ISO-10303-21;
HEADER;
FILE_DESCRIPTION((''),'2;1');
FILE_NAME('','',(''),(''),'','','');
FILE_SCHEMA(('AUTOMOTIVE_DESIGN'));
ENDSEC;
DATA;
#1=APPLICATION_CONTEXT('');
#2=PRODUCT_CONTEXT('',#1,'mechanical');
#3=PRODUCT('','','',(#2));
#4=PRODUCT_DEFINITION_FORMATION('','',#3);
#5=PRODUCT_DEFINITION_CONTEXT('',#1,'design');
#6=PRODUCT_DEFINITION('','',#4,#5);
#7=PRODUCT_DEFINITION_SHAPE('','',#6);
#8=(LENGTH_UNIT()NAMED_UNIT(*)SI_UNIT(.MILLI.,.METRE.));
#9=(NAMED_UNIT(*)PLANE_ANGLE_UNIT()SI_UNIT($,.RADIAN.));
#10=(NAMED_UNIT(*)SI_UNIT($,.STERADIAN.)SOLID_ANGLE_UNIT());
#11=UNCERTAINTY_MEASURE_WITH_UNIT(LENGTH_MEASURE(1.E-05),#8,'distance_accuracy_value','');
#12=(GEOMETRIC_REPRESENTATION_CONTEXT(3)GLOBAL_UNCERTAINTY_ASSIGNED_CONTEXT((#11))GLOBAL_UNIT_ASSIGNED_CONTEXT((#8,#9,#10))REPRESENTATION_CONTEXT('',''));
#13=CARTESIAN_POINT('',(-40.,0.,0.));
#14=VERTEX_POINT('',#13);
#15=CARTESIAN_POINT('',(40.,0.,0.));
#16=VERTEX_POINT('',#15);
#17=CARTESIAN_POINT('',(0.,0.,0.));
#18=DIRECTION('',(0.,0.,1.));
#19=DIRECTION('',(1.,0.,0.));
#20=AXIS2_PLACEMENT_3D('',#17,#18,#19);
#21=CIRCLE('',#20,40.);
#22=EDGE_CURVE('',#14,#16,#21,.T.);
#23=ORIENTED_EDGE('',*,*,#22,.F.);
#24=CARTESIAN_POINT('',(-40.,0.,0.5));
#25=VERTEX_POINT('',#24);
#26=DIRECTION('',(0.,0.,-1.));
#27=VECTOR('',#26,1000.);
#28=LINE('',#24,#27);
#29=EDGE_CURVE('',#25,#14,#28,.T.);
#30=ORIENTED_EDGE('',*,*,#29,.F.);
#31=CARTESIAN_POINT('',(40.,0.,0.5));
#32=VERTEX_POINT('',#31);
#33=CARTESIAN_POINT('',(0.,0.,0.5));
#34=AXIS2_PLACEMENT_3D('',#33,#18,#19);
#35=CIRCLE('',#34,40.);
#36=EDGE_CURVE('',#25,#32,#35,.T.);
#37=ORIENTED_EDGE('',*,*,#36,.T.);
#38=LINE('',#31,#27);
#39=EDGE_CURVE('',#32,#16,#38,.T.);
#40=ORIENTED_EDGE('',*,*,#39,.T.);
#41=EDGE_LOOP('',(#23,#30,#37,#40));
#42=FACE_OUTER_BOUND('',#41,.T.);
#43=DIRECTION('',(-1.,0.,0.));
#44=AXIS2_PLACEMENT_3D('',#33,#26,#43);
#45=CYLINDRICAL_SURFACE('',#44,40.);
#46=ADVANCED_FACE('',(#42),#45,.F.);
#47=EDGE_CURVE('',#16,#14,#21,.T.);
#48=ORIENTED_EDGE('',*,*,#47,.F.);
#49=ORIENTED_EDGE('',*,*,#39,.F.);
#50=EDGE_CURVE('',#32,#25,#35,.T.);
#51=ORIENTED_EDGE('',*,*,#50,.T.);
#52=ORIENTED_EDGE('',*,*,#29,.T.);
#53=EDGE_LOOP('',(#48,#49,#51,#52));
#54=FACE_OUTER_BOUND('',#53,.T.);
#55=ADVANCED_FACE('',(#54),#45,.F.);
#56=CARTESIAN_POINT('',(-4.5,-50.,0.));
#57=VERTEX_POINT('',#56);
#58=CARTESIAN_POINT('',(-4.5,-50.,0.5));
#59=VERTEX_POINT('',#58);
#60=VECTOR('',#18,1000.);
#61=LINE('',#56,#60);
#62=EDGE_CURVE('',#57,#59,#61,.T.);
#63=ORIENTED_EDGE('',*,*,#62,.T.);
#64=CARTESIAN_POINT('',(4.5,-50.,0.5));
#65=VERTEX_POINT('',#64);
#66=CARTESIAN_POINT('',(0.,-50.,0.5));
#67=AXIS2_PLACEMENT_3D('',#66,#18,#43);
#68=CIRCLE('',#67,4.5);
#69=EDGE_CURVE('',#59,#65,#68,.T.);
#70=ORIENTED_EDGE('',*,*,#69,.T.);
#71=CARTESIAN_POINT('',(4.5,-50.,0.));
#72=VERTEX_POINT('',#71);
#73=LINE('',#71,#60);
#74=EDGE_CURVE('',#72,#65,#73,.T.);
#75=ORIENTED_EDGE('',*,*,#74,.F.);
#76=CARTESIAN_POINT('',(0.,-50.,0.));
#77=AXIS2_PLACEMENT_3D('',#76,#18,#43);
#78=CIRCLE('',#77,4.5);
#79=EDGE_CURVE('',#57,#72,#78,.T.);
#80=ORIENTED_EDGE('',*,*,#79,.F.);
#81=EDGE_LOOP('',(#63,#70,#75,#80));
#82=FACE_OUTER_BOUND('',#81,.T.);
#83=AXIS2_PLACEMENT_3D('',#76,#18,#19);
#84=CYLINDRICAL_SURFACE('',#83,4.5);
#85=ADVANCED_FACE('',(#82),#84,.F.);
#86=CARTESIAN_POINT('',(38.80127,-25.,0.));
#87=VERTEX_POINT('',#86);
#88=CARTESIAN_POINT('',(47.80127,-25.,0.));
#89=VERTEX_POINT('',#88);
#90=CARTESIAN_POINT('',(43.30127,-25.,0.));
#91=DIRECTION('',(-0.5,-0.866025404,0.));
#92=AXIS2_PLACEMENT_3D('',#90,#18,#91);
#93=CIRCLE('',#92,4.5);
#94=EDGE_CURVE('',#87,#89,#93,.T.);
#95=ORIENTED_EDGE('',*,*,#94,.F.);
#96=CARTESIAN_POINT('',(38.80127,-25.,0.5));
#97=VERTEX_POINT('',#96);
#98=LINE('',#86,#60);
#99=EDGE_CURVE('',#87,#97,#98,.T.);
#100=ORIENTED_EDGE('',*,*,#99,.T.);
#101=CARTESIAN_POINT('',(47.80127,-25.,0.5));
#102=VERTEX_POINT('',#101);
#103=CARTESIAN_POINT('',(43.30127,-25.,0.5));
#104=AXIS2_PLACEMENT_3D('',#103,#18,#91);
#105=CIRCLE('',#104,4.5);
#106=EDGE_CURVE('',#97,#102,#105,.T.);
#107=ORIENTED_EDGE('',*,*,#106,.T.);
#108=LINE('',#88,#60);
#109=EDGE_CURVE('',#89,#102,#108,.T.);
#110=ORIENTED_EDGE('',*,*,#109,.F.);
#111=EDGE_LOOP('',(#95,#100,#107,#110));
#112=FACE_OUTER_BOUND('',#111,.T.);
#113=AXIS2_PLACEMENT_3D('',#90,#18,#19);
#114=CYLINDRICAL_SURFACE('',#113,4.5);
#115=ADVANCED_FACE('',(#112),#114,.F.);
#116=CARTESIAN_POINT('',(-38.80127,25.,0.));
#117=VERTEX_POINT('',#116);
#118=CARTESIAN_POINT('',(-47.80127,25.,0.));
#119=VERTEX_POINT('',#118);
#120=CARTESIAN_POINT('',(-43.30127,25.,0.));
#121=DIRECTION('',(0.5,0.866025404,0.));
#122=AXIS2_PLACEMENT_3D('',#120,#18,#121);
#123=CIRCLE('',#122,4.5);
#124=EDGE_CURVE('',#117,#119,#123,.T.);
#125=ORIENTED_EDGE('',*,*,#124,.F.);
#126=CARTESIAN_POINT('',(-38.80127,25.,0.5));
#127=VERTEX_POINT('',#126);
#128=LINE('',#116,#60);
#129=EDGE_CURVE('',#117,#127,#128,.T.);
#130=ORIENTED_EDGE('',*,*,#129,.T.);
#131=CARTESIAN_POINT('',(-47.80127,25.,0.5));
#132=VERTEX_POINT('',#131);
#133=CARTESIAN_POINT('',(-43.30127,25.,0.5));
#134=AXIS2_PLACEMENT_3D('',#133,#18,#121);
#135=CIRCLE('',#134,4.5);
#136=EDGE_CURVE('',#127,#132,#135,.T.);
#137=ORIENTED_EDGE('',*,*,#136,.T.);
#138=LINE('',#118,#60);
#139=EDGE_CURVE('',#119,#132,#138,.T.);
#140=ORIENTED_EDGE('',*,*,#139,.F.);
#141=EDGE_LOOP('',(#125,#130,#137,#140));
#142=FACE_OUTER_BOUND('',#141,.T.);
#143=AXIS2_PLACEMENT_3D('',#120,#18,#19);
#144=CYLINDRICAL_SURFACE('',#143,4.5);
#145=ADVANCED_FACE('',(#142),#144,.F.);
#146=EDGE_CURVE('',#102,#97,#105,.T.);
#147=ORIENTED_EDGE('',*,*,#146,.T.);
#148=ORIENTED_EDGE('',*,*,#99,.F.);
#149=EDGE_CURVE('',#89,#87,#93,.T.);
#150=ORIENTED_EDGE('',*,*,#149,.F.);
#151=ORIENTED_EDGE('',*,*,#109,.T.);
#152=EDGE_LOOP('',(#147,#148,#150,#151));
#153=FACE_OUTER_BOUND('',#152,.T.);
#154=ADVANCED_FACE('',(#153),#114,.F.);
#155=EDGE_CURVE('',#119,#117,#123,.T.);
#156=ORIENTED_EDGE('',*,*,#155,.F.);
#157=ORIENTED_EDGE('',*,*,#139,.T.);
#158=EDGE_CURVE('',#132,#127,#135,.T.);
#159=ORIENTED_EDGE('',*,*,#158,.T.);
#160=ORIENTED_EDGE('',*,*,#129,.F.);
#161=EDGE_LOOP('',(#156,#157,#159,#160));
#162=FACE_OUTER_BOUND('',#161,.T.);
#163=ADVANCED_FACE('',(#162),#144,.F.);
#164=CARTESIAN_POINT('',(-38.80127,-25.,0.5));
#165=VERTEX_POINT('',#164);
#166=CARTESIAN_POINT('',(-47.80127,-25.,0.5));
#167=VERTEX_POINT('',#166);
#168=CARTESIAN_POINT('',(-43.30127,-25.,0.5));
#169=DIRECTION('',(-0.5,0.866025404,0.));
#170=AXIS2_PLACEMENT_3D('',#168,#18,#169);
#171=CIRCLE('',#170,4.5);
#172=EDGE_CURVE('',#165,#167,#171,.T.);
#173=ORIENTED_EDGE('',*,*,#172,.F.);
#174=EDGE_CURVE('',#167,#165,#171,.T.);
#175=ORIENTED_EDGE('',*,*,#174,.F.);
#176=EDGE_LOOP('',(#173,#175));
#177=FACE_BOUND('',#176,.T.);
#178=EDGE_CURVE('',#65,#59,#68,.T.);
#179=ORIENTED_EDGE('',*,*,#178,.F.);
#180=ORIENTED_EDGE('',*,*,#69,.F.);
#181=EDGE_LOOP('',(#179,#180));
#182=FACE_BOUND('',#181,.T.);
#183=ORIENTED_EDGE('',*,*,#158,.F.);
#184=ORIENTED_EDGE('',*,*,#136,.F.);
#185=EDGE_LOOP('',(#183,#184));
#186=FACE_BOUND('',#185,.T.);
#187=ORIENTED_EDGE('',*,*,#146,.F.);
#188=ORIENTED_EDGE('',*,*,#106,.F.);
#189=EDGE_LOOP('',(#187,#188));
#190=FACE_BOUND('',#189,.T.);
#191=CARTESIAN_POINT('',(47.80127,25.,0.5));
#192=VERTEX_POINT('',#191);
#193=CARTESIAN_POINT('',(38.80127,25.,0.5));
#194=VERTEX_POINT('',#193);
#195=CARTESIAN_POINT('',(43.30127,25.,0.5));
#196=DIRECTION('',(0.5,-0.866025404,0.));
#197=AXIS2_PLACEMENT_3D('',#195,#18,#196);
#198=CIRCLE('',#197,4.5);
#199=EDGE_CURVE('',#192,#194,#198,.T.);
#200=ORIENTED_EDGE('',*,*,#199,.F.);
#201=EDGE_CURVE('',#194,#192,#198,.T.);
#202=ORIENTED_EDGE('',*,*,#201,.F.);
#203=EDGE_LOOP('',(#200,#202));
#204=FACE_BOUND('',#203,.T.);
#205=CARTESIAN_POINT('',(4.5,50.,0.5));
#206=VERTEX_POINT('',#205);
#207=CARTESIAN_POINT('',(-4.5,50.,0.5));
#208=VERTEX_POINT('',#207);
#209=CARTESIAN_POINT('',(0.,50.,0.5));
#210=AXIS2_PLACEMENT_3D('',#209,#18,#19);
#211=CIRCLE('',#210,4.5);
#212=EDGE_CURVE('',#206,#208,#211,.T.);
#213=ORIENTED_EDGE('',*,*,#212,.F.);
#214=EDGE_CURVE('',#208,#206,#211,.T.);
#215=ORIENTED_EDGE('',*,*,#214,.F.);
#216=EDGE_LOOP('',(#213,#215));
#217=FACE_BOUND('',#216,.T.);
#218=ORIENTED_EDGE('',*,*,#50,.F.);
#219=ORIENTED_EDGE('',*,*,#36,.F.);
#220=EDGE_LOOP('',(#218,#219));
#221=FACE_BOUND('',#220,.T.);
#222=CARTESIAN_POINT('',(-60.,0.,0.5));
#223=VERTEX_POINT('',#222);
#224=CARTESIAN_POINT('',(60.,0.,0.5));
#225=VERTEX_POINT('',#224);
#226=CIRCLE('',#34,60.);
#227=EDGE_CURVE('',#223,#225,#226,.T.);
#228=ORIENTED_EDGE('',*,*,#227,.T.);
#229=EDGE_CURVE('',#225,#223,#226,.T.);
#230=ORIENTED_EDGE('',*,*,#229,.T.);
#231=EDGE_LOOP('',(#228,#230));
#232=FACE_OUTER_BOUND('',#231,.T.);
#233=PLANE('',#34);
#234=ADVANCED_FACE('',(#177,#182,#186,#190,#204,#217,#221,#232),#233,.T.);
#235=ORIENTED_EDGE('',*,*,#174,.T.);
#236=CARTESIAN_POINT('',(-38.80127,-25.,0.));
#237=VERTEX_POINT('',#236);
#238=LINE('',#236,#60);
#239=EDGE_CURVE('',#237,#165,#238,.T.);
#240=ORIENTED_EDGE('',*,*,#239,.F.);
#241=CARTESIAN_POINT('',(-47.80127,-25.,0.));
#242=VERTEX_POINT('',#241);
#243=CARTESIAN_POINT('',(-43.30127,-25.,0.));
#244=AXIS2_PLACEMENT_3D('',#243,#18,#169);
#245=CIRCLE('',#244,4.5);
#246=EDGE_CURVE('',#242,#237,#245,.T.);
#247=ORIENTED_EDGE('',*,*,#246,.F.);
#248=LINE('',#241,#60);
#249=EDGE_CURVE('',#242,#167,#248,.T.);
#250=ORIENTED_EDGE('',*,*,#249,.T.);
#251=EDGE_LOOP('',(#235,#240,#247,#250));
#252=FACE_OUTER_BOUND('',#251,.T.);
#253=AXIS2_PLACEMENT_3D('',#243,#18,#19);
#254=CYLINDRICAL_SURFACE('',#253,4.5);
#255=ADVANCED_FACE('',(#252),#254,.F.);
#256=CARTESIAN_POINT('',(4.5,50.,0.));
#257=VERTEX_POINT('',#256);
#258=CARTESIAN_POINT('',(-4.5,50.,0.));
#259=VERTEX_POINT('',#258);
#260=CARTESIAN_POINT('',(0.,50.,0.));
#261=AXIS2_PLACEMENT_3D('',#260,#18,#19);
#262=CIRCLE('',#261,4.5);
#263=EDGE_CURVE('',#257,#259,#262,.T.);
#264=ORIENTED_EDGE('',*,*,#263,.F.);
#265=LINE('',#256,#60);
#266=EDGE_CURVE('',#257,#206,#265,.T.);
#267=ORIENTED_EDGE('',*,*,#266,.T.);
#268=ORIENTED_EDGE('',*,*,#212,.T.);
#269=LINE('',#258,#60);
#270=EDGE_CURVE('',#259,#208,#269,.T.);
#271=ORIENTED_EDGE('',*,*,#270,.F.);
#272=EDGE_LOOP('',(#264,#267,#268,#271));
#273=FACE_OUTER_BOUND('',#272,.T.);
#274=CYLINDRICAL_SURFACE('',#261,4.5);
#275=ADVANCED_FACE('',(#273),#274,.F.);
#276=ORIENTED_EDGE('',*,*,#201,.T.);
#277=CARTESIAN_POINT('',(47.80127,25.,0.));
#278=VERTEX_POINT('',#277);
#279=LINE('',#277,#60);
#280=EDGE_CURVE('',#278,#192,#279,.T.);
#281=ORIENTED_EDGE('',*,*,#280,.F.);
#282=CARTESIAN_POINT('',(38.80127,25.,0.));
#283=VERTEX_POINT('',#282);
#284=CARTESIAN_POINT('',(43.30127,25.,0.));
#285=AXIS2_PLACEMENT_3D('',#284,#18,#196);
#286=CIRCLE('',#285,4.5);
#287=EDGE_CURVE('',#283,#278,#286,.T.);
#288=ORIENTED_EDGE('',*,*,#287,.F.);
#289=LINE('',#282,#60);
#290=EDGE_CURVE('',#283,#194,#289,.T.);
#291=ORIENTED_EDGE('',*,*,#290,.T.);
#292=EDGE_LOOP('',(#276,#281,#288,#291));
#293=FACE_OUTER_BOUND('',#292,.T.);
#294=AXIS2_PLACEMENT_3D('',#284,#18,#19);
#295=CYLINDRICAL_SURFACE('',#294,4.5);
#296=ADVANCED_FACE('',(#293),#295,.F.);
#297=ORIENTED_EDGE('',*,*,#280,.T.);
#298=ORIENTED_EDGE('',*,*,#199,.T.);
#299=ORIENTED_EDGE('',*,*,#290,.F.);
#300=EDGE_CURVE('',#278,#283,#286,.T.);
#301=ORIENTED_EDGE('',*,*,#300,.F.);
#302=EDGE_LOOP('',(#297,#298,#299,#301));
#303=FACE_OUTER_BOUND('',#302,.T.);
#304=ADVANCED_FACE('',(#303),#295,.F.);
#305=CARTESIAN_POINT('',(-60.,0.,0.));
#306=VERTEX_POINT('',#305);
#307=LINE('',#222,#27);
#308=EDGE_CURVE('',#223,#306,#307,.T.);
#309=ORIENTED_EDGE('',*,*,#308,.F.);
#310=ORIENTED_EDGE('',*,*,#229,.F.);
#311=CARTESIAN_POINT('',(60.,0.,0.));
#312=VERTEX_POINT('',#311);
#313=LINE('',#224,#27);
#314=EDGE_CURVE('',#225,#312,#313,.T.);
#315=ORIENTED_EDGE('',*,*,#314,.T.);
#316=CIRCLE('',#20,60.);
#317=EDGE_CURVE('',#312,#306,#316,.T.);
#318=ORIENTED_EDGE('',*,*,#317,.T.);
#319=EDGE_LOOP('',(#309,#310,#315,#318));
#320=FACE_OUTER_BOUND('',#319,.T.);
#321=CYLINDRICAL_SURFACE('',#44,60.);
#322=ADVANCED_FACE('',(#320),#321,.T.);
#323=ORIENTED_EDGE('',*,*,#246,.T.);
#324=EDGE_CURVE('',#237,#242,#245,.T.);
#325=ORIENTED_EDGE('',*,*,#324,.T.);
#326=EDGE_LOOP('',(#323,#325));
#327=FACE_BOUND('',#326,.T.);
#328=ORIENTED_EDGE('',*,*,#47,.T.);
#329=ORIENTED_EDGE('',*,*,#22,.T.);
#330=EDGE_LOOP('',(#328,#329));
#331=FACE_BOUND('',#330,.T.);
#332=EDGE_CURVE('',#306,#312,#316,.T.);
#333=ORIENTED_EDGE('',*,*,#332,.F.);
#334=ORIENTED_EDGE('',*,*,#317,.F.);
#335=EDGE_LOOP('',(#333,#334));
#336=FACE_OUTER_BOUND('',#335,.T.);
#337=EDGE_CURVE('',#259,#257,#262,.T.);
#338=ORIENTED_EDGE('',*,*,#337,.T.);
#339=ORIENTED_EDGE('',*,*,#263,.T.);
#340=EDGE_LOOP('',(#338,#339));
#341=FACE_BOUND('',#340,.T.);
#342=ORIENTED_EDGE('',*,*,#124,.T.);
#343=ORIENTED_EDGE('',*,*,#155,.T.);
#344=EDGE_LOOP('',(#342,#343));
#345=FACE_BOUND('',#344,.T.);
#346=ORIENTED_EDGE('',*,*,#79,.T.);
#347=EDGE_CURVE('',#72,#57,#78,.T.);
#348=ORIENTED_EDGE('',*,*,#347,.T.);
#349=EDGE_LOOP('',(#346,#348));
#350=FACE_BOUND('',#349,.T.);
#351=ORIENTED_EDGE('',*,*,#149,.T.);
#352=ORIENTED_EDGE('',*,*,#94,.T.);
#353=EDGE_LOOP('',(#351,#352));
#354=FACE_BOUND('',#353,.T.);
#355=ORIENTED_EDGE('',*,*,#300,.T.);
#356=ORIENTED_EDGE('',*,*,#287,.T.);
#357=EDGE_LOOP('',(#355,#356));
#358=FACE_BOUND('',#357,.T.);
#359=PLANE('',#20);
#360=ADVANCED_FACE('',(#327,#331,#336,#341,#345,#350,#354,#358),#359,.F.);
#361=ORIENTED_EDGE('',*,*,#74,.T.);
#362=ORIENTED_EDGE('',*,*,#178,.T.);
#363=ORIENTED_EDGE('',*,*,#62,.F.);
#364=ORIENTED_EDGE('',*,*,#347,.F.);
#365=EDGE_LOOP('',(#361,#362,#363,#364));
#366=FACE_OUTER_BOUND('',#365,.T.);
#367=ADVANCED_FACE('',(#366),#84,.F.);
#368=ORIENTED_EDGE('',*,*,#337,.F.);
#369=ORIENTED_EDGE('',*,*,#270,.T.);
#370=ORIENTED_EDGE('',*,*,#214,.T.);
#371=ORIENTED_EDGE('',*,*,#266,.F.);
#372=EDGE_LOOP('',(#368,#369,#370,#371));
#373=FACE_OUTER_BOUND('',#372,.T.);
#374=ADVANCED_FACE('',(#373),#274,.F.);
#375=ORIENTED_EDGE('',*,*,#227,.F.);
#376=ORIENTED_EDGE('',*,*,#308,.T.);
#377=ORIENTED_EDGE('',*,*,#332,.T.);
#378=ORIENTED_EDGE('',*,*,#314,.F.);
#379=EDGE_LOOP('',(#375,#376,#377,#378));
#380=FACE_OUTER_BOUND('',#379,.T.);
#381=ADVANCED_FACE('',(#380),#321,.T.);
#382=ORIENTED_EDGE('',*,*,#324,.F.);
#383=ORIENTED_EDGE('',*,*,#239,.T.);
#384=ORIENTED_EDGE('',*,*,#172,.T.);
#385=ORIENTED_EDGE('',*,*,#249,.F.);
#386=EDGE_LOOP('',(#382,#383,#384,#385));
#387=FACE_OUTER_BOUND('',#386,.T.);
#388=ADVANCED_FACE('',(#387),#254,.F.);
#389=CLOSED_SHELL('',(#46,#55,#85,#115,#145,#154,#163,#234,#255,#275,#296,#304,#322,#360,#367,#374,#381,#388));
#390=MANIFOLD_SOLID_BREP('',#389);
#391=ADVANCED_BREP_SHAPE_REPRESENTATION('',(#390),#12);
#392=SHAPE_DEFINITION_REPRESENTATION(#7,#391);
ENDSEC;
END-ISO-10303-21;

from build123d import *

# Parameters (mm, degrees)
SKETCH1_R           = 60
SKETCH1_R_2         = 40
BOSS_EXTRUDE1_DEPTH = 0.5
SKETCH2_R           = 4.5
CUT_EXTRUDE1_DEPTH  = 85.854286869
CIRPATTERN1_COUNT   = 6


with BuildPart() as part:
    # Sketch1 → Boss-Extrude1 (new body)
    with BuildSketch(Plane.XY):
        Circle(SKETCH1_R)
        Circle(SKETCH1_R_2, mode=Mode.SUBTRACT)
    extrude(amount=BOSS_EXTRUDE1_DEPTH)

    # Sketch2 → Cut-Extrude1 (cut, through all)
    with BuildSketch(Plane.XY.offset(0.5)):
        with Locations((0, 50)):
            Circle(SKETCH2_R)
    cut_extrude1 = extrude(amount=-CUT_EXTRUDE1_DEPTH, mode=Mode.SUBTRACT)

    # CirPattern1: Cut-Extrude1 ×6 about axis
    cirpattern1_axis = Axis((0, 0, 0), (0, 0, 1))
    for i in range(1, CIRPATTERN1_COUNT):
        add(cut_extrude1.rotate(cirpattern1_axis, i * 360 / CIRPATTERN1_COUNT), mode=Mode.SUBTRACT)


solid = part.part
